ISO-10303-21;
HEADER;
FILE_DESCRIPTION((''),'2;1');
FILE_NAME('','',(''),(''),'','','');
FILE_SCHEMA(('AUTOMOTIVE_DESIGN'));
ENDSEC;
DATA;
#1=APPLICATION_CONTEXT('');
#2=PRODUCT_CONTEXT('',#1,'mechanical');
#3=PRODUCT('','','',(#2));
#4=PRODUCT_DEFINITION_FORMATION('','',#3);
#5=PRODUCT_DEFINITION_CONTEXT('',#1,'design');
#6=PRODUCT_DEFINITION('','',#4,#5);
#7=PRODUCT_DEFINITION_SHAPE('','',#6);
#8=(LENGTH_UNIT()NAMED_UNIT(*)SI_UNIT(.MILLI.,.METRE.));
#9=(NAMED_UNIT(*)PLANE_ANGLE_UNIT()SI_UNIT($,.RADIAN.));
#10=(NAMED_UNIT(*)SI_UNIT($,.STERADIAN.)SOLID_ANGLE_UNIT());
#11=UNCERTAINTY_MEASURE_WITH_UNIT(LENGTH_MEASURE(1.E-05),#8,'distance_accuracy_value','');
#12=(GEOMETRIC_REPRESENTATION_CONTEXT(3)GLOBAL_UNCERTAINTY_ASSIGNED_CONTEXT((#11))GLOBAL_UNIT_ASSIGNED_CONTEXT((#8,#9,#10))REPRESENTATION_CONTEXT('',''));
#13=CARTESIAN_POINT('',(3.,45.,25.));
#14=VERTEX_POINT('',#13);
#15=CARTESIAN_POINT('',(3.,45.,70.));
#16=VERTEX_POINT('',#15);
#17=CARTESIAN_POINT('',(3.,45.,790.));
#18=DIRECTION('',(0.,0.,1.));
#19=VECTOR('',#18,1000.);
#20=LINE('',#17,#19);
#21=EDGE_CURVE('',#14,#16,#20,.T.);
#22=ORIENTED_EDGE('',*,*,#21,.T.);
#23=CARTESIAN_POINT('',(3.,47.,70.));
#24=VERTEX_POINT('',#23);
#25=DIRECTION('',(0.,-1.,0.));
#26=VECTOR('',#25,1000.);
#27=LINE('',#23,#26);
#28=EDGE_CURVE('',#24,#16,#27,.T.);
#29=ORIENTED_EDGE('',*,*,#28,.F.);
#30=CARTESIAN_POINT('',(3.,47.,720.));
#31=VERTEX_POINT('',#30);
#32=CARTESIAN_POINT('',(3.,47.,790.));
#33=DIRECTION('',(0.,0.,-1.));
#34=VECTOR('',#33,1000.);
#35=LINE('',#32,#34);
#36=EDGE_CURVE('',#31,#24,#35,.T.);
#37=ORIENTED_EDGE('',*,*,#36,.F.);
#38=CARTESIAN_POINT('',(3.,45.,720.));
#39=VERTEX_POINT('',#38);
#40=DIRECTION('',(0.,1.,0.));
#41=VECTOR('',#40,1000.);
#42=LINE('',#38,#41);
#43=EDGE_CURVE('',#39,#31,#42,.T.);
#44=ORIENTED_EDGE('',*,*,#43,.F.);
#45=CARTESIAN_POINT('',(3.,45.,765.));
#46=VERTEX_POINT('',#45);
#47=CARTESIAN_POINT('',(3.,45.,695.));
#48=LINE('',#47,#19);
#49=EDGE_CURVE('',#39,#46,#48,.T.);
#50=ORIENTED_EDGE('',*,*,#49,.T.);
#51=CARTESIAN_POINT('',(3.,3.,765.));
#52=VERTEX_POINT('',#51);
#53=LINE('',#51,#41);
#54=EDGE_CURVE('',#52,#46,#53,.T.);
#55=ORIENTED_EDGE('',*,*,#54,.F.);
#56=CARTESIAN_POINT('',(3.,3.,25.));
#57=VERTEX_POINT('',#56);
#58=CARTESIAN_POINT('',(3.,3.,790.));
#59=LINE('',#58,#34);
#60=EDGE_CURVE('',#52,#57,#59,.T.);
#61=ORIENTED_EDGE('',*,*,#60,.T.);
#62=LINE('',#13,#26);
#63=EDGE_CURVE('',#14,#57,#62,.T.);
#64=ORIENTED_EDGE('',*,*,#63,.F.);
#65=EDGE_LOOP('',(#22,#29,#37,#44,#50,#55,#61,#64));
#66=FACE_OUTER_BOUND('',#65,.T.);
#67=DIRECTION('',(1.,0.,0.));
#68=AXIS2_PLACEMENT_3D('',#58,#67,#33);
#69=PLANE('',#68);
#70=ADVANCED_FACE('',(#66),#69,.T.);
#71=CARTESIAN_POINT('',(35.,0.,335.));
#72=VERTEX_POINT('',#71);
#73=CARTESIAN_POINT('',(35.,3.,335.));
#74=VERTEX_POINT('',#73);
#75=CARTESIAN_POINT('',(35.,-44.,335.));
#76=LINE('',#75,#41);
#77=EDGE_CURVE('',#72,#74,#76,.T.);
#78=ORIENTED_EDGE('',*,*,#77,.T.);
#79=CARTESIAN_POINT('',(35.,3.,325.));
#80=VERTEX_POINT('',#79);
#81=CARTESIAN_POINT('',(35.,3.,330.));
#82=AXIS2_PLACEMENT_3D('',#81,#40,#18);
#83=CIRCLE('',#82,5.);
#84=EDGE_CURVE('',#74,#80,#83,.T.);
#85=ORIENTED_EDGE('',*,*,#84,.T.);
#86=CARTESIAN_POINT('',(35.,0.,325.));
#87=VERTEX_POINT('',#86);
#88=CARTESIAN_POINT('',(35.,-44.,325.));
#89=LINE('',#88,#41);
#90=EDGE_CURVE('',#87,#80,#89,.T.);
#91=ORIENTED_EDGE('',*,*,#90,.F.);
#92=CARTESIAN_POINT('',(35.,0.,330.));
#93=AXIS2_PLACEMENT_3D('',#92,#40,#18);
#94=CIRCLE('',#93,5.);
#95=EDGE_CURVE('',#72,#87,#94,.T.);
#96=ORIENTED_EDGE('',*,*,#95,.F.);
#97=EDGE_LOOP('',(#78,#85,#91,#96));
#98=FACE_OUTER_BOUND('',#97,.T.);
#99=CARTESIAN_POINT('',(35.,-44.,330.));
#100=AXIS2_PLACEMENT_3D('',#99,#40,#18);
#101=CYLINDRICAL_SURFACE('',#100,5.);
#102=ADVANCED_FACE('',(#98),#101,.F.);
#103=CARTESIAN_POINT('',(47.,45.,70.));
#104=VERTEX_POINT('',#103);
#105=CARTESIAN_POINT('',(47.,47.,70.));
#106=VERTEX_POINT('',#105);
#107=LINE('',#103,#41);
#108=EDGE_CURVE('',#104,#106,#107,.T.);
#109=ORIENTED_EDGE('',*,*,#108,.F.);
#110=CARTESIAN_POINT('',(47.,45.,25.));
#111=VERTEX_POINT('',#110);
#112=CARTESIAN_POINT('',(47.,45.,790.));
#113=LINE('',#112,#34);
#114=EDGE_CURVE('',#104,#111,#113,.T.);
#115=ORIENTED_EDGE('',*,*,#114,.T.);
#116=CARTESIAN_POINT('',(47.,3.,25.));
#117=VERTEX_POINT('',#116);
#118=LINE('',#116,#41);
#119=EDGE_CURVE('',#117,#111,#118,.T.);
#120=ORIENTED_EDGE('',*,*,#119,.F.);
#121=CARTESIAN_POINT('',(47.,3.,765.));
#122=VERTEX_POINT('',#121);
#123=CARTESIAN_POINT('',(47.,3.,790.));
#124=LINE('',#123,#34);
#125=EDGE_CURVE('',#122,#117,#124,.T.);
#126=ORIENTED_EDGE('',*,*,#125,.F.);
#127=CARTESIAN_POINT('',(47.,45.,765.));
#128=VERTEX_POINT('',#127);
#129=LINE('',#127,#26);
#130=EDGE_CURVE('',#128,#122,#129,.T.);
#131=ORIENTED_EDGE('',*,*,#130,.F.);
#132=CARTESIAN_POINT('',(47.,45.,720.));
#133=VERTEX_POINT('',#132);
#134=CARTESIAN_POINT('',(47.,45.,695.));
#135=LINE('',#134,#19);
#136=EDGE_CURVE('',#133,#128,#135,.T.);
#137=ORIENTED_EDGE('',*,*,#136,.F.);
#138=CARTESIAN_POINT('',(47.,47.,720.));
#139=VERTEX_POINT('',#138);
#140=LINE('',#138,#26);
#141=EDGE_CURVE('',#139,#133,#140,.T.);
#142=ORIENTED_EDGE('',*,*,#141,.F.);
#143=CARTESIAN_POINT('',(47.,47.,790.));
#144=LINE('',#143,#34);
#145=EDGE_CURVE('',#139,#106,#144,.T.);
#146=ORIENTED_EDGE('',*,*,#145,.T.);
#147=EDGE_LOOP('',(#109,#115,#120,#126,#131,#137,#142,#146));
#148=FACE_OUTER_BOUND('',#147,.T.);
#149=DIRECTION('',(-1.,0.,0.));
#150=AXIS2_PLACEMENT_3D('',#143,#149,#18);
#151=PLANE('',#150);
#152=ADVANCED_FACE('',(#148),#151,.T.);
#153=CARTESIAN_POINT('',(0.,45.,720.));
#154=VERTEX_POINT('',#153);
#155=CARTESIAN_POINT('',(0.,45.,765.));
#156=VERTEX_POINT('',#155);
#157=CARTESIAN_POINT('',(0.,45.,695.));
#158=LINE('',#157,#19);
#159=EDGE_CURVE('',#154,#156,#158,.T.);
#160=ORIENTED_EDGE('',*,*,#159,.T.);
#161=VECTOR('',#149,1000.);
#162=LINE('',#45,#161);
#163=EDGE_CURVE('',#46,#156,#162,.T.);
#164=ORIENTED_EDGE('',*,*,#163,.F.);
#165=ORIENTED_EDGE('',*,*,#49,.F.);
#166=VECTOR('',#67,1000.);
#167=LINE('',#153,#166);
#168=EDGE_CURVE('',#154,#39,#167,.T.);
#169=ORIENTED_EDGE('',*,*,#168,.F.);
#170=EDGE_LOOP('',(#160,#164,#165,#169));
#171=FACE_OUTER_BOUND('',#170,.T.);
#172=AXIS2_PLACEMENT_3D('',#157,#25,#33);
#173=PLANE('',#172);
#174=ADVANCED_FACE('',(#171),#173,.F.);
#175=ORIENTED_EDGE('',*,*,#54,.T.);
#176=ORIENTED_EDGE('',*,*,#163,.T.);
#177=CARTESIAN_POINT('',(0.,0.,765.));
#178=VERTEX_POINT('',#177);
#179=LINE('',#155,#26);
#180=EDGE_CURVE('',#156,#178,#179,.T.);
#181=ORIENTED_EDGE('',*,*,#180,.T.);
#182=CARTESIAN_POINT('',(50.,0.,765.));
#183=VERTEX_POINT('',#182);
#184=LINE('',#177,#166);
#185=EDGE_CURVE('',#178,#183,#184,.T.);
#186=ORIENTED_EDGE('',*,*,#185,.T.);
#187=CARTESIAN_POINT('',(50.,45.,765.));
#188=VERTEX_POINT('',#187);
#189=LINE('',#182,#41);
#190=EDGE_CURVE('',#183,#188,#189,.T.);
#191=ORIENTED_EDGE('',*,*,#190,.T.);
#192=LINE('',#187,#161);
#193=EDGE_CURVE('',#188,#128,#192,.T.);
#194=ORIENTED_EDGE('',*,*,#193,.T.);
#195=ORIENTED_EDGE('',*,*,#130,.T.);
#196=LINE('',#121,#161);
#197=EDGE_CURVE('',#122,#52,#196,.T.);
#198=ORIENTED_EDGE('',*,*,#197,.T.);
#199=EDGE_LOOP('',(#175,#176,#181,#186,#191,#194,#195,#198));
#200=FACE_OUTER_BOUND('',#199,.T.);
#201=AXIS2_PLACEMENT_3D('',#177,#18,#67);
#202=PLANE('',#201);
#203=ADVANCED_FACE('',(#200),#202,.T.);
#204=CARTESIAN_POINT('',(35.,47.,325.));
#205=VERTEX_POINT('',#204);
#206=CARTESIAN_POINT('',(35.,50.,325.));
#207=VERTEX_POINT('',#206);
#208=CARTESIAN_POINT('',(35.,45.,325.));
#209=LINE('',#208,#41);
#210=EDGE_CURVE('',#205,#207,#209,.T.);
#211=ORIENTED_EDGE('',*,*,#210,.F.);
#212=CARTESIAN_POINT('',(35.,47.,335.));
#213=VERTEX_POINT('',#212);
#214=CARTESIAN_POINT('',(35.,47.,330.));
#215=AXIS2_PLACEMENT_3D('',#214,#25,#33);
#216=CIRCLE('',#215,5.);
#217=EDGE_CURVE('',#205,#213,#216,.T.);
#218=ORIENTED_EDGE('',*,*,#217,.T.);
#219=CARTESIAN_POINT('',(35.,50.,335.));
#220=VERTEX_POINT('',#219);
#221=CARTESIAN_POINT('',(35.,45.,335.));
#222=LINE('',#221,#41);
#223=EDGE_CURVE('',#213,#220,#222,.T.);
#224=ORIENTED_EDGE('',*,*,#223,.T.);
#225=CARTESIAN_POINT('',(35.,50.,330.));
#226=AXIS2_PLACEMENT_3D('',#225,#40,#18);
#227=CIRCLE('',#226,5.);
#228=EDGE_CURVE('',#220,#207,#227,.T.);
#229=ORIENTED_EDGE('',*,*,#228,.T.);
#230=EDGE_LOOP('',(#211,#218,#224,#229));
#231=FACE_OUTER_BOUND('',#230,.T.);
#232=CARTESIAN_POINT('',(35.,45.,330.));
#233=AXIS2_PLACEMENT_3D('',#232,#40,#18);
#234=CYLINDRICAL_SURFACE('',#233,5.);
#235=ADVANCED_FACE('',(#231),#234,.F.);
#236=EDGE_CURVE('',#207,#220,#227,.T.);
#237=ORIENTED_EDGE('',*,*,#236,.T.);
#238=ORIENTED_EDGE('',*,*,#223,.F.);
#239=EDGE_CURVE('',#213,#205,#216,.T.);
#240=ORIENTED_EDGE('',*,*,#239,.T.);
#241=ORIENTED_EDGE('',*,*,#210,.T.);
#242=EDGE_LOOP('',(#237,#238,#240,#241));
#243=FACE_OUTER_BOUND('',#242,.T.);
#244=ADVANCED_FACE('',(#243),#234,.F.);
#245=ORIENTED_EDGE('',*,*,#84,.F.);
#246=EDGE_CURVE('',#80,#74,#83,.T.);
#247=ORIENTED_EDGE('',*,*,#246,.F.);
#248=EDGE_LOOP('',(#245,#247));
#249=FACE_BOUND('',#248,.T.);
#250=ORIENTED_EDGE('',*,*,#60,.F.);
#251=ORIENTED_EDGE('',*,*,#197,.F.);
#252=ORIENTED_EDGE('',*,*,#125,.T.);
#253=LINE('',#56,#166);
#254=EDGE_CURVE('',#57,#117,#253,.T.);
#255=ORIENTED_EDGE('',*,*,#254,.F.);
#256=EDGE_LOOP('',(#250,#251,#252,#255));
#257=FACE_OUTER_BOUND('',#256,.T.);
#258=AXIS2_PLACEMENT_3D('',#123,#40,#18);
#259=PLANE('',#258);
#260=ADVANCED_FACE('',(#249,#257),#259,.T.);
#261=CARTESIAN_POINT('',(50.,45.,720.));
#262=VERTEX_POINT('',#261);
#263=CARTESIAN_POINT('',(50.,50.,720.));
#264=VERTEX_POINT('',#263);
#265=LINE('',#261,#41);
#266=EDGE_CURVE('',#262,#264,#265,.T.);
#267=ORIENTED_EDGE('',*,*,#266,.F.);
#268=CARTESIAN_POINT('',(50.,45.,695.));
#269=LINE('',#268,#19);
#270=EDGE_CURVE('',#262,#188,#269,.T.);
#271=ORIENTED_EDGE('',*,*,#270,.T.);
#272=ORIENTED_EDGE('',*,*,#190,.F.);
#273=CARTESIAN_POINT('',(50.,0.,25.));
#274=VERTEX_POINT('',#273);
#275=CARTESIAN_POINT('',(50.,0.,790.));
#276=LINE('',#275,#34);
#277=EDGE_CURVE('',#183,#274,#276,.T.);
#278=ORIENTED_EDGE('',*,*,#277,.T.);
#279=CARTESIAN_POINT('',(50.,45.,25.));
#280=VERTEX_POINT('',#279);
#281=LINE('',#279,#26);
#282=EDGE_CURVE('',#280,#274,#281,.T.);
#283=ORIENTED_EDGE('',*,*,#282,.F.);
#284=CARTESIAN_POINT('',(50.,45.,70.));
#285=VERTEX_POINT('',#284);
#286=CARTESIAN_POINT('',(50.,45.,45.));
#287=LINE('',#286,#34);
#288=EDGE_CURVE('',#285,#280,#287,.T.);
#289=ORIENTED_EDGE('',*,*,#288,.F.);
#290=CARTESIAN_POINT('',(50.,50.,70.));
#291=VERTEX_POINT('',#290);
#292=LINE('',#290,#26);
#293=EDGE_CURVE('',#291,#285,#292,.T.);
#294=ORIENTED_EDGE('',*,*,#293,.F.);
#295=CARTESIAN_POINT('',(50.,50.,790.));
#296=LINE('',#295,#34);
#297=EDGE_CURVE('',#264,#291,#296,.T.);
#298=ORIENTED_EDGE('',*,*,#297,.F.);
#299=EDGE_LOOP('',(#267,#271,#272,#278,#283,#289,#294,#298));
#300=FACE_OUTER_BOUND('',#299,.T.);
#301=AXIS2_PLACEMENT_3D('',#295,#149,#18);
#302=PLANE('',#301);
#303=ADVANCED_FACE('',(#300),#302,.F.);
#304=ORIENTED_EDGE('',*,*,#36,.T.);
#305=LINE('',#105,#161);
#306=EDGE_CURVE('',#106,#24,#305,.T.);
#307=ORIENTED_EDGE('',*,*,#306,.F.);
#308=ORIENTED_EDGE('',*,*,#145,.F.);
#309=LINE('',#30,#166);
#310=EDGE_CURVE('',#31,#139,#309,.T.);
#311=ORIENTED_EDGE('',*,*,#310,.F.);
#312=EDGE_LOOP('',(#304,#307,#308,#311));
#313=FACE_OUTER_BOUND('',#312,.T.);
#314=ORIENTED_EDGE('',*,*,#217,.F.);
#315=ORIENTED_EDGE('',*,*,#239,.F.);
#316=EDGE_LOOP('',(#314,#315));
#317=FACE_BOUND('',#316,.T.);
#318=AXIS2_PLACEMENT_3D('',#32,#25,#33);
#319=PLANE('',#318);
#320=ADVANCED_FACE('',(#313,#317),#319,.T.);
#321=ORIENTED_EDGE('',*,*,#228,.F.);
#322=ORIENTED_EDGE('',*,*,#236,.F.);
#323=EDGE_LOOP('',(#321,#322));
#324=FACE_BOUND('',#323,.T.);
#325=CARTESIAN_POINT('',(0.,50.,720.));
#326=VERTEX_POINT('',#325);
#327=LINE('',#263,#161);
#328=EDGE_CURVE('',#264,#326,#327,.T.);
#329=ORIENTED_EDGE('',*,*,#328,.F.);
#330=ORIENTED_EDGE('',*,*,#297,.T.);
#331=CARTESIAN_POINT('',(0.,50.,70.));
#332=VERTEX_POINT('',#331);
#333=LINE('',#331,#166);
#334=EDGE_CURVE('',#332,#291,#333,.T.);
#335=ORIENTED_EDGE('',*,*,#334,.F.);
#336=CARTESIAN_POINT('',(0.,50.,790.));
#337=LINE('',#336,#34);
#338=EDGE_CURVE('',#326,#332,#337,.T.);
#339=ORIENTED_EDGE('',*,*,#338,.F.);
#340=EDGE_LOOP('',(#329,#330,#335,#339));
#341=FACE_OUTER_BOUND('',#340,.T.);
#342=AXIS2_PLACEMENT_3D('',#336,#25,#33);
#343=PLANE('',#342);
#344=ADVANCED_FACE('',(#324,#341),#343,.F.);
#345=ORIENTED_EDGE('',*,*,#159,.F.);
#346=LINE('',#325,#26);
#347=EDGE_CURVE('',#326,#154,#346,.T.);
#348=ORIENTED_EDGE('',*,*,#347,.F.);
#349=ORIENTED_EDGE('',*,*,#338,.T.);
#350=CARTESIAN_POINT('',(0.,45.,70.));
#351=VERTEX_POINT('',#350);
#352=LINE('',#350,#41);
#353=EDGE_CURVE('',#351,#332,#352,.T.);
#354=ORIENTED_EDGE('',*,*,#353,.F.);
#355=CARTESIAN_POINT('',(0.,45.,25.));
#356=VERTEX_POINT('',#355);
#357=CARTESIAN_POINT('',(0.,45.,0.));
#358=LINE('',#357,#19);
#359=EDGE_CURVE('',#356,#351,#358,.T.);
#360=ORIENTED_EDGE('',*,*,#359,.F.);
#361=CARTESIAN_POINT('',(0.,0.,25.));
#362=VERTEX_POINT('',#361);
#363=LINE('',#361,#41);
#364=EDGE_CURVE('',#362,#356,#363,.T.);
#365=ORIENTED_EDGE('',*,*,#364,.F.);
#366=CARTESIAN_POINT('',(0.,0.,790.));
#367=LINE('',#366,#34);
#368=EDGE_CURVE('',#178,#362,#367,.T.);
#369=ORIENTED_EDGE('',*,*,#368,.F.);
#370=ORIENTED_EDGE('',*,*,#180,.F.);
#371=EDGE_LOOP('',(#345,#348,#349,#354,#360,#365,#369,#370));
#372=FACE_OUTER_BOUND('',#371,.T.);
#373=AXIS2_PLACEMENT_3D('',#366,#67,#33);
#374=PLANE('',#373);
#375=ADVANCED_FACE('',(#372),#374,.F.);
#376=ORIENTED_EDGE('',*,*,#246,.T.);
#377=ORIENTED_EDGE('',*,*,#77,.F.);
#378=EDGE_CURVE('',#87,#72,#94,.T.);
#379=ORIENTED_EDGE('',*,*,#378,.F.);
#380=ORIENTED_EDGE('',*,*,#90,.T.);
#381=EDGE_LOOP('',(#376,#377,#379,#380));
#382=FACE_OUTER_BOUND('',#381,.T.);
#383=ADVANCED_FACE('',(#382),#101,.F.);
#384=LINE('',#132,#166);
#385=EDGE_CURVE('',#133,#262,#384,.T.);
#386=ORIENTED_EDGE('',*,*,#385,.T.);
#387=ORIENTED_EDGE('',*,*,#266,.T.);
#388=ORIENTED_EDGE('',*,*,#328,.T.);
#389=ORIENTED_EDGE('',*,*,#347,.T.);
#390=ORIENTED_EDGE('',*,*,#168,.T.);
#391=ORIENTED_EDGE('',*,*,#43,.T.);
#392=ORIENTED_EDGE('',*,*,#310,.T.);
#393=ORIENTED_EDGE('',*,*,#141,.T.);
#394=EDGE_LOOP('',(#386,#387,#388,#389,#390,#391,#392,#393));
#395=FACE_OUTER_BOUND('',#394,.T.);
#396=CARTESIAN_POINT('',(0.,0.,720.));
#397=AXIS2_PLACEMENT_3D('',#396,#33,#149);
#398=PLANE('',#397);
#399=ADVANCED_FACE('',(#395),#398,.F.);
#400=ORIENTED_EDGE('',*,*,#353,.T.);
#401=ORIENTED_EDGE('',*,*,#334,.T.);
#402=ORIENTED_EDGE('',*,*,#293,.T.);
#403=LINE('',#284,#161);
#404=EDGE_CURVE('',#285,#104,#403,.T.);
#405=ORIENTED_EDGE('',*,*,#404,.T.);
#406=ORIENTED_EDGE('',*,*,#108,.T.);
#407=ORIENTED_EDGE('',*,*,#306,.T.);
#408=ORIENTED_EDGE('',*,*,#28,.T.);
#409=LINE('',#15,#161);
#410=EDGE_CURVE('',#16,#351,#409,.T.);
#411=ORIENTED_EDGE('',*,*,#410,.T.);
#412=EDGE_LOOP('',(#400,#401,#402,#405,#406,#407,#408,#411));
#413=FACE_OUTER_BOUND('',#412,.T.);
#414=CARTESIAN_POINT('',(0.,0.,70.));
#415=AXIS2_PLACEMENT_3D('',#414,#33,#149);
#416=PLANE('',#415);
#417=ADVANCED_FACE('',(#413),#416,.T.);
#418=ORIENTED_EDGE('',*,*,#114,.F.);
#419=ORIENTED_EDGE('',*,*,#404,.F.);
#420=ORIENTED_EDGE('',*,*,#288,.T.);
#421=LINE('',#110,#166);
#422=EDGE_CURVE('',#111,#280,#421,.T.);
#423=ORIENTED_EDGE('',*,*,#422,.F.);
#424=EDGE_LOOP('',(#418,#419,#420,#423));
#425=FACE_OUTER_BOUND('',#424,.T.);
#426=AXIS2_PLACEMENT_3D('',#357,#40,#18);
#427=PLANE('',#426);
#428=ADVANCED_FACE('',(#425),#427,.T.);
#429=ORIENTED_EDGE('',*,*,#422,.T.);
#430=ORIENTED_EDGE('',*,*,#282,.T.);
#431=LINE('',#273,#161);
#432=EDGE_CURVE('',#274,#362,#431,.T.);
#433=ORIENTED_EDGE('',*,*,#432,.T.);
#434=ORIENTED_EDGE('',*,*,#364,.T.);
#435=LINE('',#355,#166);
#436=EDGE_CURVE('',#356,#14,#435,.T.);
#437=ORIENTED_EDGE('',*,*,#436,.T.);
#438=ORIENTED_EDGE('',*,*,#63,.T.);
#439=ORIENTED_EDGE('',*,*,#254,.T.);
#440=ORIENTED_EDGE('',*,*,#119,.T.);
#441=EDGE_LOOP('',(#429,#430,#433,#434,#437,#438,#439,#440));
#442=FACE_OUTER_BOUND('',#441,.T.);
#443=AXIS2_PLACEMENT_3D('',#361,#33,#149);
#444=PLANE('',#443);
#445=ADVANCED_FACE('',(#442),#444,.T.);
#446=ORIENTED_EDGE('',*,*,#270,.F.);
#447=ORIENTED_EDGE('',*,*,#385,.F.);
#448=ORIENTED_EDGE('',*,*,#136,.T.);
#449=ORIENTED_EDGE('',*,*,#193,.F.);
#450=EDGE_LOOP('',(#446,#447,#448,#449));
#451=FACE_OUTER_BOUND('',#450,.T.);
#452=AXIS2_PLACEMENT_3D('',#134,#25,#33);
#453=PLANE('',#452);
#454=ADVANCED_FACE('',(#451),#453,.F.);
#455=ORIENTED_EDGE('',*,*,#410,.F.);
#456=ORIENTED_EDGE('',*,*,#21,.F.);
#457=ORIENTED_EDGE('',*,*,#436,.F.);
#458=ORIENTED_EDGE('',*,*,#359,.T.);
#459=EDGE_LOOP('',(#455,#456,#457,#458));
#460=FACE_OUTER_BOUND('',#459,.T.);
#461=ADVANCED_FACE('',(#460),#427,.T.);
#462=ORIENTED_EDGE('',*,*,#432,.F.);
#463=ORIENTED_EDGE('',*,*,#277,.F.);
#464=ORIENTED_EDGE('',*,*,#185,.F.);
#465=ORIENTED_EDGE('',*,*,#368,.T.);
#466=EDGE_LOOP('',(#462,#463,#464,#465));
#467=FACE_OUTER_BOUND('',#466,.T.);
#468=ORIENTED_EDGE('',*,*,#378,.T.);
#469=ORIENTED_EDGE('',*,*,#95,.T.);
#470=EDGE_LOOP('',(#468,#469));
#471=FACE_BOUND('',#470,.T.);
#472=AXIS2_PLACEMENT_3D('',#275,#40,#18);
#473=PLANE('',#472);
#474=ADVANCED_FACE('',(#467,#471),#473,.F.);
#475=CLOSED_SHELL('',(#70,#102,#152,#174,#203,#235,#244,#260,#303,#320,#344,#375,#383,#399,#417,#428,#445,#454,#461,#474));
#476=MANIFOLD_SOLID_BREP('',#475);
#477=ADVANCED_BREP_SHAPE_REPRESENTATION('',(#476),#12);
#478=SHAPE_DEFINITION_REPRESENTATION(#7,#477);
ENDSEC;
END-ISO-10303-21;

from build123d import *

# Parameters (mm, degrees)
SKETCH_1_W          = 50
SKETCH_1_H          = 50
SKETCH_1_W_2        = 44
SKETCH_1_H_2        = 44
EXTRUDE_1_DEPTH     = 790
SKETCH_2_W          = 50
SKETCH_2_H          = 45
CUT_EXTRUDE_1_DEPTH = 5
SKETCH_3_R          = 5
CUT_EXTRUDE_2_DEPTH = 5
CUT_EXTRUDE_3_DEPTH = 50
CUT_EXTRUDE_4_DEPTH = 50
EXTRUDE_2_DEPTH     = 25
EXTRUDE_3_DEPTH     = 25
CUT_EXTRUDE_5_DEPTH = 25
CUT_EXTRUDE_6_DEPTH = 25
SKETCH_10_R         = 5
CUT_EXTRUDE_7_DEPTH = 94


with BuildPart() as part:
    # 草图1 → 凸台-拉伸1 (new body)
    with BuildSketch(Plane.XY):
        with Locations((25, 25)):
            Rectangle(SKETCH_1_W, SKETCH_1_H)
        with Locations((25, 25)):
            Rectangle(SKETCH_1_W_2, SKETCH_1_H_2, mode=Mode.SUBTRACT)
    extrude(amount=EXTRUDE_1_DEPTH)

    # 草图2 → 切除-拉伸1 (cut)
    with BuildSketch(Plane(origin=(0, 50, 0), x_dir=(1, 0, 0), z_dir=(0, 1, 0))):
        with Locations((25, -22.5)):
            Rectangle(SKETCH_2_W, SKETCH_2_H)
        with Locations((25, -767.5)):
            Rectangle(SKETCH_2_W, SKETCH_2_H)
    extrude(amount=-CUT_EXTRUDE_1_DEPTH, mode=Mode.SUBTRACT)

    # 草图3 → 切除-拉伸2 (cut)
    with BuildSketch(Plane(origin=(0, 50, 0), x_dir=(1, 0, 0), z_dir=(0, 1, 0))):
        with Locations(Location((35, -330, 0), (0, 0, 270))):
            Circle(SKETCH_3_R)
    extrude(amount=-CUT_EXTRUDE_2_DEPTH, mode=Mode.SUBTRACT)

    # 草图4 → 切除-拉伸3 (cut)
    with BuildSketch(Plane.XY.offset(790)):
        Polygon((50, 0), (50, 45), (47, 45), (47, 3), (3, 3), (3, 45), (0, 45), (0, 0), align=None)
    extrude(amount=-CUT_EXTRUDE_3_DEPTH, mode=Mode.SUBTRACT)

    # 草图5 → 切除-拉伸4 (cut)
    with BuildSketch(Plane.XY.offset(745)):
        Polygon((47, 47), (47, 45), (50, 45), (50, 50), (0, 50), (0, 45), (3, 45), (3, 47), align=None)
    extrude(amount=-CUT_EXTRUDE_4_DEPTH, mode=Mode.SUBTRACT)

    # 草图6 → 凸台-拉伸2 (add)
    with BuildSketch(Plane.XY.offset(695)):
        Polygon((3, 47), (47, 47), (47, 45), (50, 45), (50, 50), (0, 50), (0, 45), (3, 45), align=None)
    extrude(amount=EXTRUDE_2_DEPTH)

    # 草图7 → 凸台-拉伸3 (add)
    with BuildSketch(Plane.XY.offset(740)):
        Polygon((0, 0), (50, 0), (50, 45), (47, 45), (47, 3), (3, 3), (3, 45), (0, 45), align=None)
    extrude(amount=EXTRUDE_3_DEPTH)

    # 草图8 → 切除-拉伸5 (cut)
    with BuildSketch(Plane(origin=(0, 0, 0), x_dir=(-1, 0, 0), z_dir=(0, 0, -1))):
        Polygon((0, 0), (0, 45), (-3, 45), (-3, 3), (-47, 3), (-47, 45), (-50, 45), (-50, 0), align=None)
    extrude(amount=-CUT_EXTRUDE_5_DEPTH, mode=Mode.SUBTRACT)

    # 草图9 → 切除-拉伸6 (cut)
    with BuildSketch(Plane(origin=(0, 0, 45), x_dir=(-1, 0, 0), z_dir=(0, 0, -1))):
        Polygon((-47, 45), (-47, 47), (-3, 47), (-3, 45), (0, 45), (0, 50), (-50, 50), (-50, 45), align=None)
    extrude(amount=-CUT_EXTRUDE_6_DEPTH, mode=Mode.SUBTRACT)

    # 草图10 → 切除-拉伸7 (cut)
    with BuildSketch(Plane(origin=(0, 50, 0), x_dir=(1, 0, 0), z_dir=(0, 1, 0))):
        with Locations(Location((35, -330, 0), (0, 0, 270))):
            Circle(SKETCH_10_R)
    extrude(amount=-CUT_EXTRUDE_7_DEPTH, mode=Mode.SUBTRACT)


solid = part.part
